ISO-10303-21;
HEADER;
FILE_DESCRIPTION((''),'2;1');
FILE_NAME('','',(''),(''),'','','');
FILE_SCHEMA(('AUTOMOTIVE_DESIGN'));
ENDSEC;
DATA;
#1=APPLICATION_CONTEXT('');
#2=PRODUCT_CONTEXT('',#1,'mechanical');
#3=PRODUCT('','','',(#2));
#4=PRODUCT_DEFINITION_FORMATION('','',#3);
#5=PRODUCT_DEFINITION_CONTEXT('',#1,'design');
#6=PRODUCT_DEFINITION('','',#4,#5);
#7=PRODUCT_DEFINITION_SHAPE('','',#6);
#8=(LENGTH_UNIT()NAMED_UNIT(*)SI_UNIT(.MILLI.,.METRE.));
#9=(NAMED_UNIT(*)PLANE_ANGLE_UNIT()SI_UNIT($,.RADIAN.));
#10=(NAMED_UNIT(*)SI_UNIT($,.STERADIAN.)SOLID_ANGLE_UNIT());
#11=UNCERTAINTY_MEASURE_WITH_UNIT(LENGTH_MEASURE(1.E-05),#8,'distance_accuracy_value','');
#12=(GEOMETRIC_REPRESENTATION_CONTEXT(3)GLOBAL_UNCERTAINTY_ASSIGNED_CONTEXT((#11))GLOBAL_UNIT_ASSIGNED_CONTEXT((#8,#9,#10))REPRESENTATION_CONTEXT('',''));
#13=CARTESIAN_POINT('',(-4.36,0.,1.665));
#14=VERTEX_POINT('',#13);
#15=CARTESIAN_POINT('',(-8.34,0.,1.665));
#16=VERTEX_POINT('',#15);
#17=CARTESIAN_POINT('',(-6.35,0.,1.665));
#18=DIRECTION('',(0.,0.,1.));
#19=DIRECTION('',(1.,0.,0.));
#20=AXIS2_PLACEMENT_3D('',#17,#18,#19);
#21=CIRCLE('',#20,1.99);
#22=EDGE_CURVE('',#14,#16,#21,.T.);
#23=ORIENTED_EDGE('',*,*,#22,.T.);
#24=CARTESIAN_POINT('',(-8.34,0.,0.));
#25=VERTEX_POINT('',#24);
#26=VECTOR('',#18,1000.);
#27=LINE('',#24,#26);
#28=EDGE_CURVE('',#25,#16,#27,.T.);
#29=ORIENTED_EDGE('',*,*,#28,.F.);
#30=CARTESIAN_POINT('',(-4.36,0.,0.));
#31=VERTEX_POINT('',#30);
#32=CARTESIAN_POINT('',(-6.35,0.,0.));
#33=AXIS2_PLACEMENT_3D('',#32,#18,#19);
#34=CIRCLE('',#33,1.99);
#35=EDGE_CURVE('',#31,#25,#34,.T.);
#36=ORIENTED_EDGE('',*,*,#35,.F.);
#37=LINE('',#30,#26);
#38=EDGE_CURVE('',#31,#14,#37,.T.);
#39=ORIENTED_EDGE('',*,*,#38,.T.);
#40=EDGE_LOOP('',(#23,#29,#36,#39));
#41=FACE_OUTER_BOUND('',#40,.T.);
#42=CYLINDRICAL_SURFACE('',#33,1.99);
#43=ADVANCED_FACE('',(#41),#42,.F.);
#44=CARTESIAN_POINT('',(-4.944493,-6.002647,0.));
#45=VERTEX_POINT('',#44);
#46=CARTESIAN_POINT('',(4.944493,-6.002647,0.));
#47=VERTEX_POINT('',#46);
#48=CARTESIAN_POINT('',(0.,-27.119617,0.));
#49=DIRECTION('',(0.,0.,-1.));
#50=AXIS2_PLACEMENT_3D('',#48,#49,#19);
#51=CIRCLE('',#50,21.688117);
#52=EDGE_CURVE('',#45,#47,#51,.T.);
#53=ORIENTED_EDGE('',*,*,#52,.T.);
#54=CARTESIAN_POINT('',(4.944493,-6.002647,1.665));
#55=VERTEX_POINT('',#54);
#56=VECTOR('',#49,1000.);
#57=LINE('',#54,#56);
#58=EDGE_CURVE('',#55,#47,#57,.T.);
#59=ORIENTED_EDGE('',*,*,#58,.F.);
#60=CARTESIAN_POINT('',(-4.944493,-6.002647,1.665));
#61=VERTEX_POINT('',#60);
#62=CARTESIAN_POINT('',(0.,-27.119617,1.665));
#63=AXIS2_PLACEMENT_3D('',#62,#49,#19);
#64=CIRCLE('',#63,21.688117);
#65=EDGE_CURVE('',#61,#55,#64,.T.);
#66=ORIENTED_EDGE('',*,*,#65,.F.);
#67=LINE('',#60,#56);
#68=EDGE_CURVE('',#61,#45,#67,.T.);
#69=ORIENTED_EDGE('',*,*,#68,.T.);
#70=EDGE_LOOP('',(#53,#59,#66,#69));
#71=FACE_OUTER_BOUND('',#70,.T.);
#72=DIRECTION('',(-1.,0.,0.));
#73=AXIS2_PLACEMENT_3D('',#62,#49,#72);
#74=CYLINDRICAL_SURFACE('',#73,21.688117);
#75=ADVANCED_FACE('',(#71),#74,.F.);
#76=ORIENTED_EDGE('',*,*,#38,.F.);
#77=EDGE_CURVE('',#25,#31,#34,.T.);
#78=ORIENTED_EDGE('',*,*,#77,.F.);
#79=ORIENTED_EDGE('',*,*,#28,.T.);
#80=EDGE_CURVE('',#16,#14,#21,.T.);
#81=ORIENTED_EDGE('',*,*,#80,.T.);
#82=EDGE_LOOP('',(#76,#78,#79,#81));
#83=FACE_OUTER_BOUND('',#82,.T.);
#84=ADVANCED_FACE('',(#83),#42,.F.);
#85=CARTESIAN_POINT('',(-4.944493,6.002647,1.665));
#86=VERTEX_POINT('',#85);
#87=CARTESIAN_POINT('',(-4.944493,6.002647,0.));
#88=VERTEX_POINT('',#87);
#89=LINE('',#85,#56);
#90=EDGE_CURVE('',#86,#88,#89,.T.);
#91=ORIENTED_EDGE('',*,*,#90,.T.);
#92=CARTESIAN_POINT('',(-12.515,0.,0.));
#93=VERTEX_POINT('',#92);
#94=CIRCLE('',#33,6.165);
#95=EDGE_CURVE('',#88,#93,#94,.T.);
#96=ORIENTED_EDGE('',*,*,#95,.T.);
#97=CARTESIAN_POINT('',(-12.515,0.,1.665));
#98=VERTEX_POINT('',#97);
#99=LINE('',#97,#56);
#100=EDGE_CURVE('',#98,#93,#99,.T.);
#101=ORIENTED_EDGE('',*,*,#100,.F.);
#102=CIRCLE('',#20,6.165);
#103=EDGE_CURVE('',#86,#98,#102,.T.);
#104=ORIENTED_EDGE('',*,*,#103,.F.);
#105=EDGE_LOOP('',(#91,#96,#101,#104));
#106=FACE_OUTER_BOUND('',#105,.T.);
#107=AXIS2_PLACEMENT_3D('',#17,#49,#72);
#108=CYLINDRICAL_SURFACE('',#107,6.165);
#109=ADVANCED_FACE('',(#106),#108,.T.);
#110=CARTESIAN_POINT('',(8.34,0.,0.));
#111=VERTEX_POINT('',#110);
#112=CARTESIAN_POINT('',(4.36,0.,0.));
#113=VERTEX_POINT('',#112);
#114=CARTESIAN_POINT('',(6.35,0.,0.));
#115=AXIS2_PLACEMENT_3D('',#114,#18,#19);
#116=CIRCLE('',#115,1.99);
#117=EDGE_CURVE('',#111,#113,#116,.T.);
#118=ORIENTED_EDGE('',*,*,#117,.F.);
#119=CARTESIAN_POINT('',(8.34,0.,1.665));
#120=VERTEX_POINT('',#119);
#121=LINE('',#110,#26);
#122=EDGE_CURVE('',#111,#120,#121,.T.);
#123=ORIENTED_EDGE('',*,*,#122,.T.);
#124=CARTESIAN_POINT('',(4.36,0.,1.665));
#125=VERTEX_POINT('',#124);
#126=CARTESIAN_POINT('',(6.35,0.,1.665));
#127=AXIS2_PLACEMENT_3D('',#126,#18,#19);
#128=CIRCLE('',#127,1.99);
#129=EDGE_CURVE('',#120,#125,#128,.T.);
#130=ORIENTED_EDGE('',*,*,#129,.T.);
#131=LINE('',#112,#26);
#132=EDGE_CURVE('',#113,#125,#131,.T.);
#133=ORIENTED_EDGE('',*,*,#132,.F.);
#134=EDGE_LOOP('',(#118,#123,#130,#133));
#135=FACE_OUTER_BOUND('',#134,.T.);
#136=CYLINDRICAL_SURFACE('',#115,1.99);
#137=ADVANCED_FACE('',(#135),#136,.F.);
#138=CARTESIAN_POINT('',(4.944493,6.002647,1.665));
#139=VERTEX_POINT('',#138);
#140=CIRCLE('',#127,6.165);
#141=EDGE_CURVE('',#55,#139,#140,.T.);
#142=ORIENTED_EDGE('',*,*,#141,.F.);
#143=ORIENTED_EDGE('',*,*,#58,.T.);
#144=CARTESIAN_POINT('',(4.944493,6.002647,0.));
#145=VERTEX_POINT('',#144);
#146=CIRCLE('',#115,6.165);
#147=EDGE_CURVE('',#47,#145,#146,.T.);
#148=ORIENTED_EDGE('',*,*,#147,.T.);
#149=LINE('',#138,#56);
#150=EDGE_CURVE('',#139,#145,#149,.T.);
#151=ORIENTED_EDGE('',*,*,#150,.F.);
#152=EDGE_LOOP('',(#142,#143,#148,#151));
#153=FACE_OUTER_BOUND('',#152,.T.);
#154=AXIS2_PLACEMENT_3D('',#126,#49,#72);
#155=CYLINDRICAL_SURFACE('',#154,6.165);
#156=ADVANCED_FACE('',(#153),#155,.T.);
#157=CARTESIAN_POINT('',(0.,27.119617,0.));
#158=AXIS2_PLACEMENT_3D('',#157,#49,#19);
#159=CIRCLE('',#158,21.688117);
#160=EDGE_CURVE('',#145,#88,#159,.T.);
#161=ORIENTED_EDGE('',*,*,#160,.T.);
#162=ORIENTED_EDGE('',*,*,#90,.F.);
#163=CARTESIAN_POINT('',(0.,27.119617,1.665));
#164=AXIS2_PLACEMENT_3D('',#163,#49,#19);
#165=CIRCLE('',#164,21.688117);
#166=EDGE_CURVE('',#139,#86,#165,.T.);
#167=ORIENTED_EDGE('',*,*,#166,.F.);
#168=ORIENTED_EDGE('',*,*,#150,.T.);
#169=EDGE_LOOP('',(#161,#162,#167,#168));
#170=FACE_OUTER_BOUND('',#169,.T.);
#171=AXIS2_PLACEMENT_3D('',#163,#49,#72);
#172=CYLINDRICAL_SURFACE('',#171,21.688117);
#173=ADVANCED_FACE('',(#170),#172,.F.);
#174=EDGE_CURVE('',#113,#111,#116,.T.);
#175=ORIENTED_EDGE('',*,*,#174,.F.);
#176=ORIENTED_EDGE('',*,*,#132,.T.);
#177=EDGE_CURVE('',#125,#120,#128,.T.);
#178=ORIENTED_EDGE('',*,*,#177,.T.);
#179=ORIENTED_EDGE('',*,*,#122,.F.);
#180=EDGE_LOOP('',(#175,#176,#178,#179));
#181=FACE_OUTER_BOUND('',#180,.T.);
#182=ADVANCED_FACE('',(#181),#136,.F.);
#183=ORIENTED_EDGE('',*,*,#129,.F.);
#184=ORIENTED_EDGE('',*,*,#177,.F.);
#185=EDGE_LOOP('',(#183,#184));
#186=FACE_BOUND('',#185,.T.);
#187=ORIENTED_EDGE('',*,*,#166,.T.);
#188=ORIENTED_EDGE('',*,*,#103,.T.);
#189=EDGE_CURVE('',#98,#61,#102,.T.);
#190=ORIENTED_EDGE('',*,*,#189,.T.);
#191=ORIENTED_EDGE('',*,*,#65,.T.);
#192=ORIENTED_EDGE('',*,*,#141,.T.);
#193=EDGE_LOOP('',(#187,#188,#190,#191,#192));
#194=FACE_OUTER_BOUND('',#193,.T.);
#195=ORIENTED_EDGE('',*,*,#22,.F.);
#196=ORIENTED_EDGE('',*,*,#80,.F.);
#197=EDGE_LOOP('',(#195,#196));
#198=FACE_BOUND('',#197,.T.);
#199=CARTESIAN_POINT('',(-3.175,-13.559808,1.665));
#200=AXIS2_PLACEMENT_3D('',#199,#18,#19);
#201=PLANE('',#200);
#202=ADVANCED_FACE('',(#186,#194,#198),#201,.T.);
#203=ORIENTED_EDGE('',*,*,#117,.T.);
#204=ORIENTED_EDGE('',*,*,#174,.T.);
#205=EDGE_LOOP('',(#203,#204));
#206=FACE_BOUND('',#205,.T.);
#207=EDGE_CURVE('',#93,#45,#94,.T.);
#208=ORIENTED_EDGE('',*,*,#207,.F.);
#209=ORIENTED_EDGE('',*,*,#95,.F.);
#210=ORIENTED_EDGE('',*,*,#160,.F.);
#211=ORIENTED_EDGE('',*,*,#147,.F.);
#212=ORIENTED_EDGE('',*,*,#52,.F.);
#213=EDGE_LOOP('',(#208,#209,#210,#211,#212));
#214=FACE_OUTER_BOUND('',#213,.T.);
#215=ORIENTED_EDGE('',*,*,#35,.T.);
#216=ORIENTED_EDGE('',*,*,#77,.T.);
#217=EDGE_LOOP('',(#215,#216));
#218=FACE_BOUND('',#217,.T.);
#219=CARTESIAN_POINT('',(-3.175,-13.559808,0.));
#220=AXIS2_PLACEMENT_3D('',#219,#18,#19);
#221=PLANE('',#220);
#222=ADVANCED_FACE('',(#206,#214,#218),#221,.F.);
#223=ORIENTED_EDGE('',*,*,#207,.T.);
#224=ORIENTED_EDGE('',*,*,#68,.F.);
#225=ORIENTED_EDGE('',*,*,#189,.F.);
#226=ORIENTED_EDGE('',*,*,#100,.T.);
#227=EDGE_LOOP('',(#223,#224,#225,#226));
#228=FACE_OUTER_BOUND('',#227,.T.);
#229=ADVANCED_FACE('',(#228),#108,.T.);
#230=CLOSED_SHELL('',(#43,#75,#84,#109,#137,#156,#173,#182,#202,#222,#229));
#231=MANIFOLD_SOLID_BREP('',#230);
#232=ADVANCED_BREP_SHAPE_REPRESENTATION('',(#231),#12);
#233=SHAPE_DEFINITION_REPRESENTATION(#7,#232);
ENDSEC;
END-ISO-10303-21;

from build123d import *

# Parameters (mm, degrees)
EXTRUDE_1_DEPTH     = 1.665
SKETCH_3_R          = 1.99
CUT_EXTRUDE_1_DEPTH = 15.050077402


with BuildPart() as part:
    # 草图2 → 拉伸1 (new body)
    with BuildSketch(Plane.XY):
        with BuildLine():
            ThreePointArc((-4.944493019, 6.002647343), (-12.515, 0), (-4.944493019, -6.002647343))
            ThreePointArc((-4.944493019, -6.002647343), (0, -5.4315), (4.944493019, -6.002647343))
            ThreePointArc((4.944493019, -6.002647343), (12.515, 0), (4.944493019, 6.002647343))
            ThreePointArc((4.944493019, 6.002647343), (0, 5.4315), (-4.944493019, 6.002647343))
        make_face()
    extrude(amount=EXTRUDE_1_DEPTH)

    # 草图3 → 切除-拉伸1 (cut, through all)
    with BuildSketch(Plane.XY.offset(1.665)):
        with Locations((-6.35, 0)):
            Circle(SKETCH_3_R)
        with Locations((6.35, 0)):
            Circle(SKETCH_3_R)
    extrude(amount=-CUT_EXTRUDE_1_DEPTH, mode=Mode.SUBTRACT)


solid = part.part
